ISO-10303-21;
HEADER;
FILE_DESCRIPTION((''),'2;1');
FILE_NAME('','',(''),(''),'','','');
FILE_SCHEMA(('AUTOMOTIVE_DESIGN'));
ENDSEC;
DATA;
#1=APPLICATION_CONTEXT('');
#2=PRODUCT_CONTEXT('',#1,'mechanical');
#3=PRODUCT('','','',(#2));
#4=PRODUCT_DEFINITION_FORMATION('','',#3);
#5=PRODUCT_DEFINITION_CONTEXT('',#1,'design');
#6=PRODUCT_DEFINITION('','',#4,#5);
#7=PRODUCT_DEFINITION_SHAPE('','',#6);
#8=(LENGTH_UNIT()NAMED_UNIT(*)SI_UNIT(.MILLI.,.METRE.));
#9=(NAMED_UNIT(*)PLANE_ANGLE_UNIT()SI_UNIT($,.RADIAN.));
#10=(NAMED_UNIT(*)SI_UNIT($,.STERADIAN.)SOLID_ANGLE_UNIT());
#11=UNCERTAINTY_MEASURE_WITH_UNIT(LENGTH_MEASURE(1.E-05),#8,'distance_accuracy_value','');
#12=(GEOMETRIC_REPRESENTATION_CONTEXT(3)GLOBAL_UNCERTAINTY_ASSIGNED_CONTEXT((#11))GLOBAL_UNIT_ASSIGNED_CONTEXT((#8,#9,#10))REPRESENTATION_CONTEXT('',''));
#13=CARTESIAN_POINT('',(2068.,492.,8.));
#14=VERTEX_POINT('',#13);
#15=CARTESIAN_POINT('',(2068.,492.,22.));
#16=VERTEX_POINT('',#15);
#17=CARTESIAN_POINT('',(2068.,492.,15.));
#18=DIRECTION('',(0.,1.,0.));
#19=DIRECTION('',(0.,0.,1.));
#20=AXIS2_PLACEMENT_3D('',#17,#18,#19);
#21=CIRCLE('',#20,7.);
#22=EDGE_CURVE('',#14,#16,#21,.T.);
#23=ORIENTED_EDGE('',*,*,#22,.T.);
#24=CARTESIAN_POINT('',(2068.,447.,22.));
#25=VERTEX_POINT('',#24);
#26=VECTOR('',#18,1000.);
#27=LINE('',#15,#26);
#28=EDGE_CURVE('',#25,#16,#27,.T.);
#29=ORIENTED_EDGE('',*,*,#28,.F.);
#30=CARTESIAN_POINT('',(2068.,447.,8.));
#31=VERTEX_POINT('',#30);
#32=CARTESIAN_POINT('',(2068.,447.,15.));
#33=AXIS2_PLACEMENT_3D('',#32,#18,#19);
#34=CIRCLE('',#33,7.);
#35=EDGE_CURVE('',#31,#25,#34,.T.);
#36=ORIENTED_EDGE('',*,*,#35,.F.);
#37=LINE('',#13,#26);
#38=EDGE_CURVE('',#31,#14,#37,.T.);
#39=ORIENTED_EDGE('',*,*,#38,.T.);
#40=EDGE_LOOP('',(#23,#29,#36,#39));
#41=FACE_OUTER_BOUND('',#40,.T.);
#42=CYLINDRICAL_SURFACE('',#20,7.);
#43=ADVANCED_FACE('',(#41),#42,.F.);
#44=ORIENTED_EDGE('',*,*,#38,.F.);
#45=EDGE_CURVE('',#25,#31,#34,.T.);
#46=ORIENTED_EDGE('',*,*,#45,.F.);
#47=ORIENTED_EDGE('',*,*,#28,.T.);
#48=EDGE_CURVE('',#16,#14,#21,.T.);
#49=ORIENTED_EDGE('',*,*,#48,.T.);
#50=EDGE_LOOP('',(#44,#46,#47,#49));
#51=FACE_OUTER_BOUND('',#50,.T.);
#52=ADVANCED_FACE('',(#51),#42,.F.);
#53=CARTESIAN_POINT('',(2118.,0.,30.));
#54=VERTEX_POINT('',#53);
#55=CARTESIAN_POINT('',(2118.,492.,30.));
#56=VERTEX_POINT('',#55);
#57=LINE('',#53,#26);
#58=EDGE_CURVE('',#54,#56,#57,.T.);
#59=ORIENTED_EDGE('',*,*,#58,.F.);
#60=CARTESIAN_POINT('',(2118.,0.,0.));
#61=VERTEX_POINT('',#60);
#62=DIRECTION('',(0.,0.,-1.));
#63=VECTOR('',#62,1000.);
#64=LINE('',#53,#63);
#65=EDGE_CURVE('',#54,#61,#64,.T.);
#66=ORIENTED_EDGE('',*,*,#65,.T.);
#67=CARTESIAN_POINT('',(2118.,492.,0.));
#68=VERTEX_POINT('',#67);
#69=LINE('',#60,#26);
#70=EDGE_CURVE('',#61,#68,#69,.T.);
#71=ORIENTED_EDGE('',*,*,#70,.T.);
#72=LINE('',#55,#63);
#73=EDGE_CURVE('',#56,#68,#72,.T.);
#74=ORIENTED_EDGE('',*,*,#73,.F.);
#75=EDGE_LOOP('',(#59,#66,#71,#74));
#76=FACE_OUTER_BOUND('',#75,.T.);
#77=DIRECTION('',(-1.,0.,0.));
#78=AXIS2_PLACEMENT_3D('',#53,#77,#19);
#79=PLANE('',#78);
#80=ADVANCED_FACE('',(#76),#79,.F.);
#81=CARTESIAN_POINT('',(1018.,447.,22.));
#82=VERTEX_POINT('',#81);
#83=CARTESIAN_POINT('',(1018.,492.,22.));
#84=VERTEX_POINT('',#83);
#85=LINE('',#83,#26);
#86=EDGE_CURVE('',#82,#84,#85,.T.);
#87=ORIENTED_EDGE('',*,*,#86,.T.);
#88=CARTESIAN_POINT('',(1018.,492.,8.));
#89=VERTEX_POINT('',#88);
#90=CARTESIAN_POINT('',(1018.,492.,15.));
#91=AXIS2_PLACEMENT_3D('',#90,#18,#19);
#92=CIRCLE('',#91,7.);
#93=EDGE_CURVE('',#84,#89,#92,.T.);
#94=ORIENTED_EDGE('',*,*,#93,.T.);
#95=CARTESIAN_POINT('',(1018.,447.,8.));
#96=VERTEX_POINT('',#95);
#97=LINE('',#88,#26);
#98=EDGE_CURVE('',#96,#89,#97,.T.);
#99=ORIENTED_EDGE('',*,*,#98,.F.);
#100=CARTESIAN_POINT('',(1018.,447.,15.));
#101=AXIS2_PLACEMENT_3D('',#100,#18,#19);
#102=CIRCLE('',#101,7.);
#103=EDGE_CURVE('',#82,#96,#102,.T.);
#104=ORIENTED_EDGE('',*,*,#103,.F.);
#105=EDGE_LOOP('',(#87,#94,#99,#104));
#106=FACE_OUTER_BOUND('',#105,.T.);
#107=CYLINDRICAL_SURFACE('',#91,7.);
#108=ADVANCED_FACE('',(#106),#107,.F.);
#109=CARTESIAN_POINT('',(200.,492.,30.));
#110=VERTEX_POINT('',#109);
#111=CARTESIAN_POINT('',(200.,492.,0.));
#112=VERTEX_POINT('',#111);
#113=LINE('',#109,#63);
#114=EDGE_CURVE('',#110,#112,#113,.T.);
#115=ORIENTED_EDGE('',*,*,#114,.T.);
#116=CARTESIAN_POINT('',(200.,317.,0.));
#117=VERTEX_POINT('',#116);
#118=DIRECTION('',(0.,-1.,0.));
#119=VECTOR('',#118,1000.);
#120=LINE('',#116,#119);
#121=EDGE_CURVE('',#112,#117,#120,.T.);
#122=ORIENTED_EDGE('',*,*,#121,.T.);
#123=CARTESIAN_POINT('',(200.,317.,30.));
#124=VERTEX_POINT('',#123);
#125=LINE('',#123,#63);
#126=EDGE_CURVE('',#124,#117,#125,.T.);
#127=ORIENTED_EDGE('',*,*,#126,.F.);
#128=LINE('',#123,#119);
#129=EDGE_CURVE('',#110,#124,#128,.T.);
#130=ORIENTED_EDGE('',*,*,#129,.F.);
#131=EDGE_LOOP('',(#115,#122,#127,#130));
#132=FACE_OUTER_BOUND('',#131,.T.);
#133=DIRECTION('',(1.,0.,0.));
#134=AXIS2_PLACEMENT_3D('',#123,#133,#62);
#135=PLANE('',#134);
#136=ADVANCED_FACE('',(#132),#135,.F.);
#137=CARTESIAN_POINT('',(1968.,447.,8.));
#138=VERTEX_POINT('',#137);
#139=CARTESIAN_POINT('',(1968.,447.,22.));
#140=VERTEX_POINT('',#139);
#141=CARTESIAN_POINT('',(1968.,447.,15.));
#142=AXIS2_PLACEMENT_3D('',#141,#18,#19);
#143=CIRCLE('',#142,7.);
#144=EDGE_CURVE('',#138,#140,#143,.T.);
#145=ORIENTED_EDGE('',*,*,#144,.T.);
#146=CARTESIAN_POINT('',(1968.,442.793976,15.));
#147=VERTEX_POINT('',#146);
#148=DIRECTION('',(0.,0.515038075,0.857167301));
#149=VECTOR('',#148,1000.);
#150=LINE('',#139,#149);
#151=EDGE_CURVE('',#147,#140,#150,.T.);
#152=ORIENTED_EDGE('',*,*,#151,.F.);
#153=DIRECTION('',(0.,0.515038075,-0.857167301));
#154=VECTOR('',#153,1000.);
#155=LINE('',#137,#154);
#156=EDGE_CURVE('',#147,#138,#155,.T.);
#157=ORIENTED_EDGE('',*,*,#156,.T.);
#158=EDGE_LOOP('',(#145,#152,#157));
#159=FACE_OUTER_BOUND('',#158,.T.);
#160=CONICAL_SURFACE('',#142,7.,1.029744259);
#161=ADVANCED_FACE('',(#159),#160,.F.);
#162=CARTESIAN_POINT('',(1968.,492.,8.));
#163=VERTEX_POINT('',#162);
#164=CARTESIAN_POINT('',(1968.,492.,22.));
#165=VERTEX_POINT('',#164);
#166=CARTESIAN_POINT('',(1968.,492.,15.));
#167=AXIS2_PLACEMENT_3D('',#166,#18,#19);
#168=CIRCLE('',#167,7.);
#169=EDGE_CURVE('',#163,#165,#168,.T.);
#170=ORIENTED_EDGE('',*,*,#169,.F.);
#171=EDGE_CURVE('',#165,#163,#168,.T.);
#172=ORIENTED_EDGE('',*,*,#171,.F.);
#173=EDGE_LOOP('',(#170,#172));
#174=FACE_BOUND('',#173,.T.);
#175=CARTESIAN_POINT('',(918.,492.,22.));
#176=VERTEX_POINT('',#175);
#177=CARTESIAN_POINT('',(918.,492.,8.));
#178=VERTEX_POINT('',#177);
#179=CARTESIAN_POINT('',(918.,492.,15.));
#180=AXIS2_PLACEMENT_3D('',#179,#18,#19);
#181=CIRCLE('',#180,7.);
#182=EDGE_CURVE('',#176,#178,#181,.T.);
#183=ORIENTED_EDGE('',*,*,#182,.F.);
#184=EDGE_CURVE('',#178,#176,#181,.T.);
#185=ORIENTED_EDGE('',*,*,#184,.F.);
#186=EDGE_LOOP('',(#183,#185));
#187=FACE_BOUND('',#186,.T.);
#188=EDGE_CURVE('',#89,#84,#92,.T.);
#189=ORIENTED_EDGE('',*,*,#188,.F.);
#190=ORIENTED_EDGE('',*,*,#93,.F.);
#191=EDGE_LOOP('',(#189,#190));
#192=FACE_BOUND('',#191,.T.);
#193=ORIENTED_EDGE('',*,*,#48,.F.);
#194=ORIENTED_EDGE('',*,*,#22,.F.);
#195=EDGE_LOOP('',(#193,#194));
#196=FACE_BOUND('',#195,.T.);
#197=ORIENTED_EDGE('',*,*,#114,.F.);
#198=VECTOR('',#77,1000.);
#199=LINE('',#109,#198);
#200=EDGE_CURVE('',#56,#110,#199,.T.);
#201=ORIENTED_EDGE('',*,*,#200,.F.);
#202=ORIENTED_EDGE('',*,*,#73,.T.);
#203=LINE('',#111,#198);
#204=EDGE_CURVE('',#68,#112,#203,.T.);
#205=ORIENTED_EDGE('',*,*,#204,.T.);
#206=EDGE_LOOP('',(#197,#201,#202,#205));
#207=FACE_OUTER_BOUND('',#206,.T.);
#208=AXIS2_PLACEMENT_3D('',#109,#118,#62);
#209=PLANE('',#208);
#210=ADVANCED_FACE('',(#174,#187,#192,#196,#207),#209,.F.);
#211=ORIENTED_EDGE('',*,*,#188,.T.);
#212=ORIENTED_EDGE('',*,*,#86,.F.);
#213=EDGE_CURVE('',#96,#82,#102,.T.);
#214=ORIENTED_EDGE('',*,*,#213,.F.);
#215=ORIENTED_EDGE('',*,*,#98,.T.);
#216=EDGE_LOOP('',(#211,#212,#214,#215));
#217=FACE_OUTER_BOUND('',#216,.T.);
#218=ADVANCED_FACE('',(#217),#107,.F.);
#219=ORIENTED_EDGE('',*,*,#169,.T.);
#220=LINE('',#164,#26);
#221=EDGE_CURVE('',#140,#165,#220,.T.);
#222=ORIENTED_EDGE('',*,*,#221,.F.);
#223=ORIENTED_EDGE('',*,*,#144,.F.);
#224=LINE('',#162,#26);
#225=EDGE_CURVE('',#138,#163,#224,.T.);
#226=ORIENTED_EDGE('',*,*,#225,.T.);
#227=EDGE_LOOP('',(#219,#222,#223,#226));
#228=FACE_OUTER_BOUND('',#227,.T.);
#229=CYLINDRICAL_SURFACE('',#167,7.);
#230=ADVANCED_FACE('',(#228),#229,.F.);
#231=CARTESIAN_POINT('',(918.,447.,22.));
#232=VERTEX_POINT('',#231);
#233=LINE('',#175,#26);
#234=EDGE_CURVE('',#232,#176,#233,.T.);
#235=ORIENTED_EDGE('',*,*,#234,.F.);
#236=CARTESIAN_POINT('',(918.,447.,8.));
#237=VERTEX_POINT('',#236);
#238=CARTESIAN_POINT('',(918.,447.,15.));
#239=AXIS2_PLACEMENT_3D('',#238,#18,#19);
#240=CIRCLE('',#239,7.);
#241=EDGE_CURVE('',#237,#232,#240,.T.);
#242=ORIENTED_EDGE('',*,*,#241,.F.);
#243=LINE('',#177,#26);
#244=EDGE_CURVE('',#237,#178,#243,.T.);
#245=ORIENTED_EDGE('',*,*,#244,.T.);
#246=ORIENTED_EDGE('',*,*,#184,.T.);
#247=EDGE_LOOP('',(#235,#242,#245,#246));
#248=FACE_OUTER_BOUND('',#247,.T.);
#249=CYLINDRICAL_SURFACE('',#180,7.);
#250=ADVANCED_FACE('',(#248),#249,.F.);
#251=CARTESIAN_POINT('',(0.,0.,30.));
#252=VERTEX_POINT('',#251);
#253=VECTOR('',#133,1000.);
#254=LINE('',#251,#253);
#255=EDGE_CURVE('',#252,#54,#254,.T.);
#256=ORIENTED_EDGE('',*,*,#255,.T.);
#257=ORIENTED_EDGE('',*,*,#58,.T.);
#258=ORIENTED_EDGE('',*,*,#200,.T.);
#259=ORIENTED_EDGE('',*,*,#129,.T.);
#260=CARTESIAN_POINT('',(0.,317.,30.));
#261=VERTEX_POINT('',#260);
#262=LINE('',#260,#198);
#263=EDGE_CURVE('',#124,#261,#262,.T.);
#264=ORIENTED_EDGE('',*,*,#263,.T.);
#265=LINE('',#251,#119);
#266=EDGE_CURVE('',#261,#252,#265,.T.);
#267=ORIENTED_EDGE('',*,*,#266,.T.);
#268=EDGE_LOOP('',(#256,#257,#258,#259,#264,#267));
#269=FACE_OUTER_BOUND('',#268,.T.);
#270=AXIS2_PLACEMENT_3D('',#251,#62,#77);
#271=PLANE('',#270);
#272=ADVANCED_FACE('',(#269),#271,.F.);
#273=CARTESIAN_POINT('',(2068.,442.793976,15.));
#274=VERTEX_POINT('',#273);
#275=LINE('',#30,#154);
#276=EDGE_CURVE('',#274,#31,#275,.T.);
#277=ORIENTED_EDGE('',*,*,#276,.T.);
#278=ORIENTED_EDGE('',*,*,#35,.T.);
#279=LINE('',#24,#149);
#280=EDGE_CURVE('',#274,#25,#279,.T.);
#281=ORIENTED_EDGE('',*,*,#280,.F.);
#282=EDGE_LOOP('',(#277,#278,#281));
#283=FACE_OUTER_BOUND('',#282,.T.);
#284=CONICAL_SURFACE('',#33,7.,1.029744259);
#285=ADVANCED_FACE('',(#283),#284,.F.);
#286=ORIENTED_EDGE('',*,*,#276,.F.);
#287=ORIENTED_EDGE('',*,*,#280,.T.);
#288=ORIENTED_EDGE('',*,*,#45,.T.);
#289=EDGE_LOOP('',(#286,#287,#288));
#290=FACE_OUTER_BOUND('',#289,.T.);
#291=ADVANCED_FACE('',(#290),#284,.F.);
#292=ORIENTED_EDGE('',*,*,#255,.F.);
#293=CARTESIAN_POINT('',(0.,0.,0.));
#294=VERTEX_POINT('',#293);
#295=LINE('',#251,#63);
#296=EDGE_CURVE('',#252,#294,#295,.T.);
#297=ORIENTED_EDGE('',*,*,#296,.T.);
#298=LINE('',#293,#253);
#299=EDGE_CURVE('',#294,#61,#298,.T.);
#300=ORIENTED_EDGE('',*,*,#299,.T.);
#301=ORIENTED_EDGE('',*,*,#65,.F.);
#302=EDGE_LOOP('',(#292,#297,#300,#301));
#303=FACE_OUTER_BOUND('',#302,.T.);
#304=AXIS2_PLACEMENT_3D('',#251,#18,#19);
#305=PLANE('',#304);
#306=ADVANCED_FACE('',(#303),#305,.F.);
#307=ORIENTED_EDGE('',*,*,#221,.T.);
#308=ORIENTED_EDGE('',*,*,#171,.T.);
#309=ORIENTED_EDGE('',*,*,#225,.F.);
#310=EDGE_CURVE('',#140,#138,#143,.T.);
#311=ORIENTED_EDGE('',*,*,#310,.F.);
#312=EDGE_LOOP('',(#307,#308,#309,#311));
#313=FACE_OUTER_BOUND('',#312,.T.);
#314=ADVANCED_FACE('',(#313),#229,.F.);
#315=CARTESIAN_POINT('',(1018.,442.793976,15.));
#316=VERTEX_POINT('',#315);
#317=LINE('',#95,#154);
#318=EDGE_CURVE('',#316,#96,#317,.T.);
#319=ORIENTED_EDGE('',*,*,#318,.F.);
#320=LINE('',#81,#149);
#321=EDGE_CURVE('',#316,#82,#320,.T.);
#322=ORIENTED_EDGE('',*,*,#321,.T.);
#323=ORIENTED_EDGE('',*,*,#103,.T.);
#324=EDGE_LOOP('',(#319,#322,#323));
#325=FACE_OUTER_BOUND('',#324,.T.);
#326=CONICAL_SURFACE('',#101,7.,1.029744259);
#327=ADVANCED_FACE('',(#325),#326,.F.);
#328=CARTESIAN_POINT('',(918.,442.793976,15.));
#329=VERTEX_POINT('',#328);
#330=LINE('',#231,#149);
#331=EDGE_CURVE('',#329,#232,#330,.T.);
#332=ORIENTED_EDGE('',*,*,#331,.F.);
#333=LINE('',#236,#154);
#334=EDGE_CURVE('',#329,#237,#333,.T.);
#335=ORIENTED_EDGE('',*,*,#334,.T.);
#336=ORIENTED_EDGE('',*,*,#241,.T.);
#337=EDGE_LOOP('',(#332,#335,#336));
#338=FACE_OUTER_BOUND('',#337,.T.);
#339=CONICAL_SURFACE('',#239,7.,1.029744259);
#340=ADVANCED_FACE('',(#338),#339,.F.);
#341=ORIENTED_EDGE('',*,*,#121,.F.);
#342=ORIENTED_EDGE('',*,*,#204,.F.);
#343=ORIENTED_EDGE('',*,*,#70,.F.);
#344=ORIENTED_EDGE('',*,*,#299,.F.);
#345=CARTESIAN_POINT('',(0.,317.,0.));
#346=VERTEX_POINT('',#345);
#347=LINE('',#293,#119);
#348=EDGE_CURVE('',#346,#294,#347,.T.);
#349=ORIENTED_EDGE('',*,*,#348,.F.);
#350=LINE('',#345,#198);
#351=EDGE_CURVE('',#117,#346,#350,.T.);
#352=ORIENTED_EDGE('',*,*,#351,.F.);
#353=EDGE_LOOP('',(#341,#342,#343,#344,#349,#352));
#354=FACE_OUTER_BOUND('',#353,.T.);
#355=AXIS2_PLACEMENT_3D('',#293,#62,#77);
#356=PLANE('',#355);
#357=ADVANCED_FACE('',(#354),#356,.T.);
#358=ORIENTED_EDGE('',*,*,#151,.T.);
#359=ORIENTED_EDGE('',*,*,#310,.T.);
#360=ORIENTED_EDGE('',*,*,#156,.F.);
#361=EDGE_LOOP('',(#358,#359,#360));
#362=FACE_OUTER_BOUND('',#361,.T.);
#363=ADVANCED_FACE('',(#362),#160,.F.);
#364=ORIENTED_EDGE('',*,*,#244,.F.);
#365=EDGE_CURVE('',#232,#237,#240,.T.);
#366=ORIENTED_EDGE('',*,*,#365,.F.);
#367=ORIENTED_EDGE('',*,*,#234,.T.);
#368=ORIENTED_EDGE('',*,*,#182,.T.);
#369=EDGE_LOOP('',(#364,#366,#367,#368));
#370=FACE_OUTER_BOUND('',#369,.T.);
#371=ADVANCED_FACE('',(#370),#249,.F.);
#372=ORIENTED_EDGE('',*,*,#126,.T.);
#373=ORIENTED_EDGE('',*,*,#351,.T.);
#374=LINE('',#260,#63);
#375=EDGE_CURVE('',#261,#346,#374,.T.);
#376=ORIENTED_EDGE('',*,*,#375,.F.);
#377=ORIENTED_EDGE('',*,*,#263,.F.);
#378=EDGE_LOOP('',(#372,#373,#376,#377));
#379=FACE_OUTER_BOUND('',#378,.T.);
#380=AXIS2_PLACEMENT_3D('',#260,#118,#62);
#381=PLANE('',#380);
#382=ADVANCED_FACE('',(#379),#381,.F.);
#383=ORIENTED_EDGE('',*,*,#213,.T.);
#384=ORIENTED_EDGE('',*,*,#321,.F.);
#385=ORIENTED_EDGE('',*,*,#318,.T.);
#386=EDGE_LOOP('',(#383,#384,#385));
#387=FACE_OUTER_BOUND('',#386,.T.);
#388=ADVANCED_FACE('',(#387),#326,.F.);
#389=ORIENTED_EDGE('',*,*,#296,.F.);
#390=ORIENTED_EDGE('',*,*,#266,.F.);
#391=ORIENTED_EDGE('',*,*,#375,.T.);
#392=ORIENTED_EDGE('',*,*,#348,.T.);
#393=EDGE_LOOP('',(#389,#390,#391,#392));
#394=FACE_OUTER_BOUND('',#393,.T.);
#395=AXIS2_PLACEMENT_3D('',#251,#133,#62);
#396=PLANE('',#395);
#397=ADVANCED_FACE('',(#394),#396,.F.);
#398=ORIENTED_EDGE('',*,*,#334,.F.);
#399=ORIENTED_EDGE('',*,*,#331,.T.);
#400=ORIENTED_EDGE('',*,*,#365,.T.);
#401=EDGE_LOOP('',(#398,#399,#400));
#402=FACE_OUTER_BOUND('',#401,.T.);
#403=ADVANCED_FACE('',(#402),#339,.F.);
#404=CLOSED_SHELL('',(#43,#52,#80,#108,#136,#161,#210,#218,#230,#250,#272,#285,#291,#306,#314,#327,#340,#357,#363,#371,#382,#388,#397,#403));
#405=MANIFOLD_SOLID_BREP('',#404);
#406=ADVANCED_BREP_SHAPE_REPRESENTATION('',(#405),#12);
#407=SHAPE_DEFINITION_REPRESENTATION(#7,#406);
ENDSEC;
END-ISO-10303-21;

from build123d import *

# Parameters (mm, degrees)
BOSS_EXTRUDE1_DEPTH    = 30
M16_TAPPED_HOLE1_D     = 14
M16_TAPPED_HOLE1_DEPTH = 45
M16_TAPPED_HOLE1_TIP   = 4.206024333


with BuildPart() as part:
    # Sketch1 → Boss-Extrude1 (new body)
    with BuildSketch(Plane.XY):
        Polygon((0, 317), (200, 317), (200, 492), (2118, 492), (2118, 0), (0, 0), align=None)
    extrude(amount=BOSS_EXTRUDE1_DEPTH)

    # M16 Tapped Hole1
    with Locations(Plane(origin=(918, 492, 15), x_dir=(0, 0, 1), z_dir=(0, 1, 0))):
        with Locations((0, 0), (0, 100), (0, 1150), (0, 1050)):
            Hole(M16_TAPPED_HOLE1_D / 2, depth=M16_TAPPED_HOLE1_DEPTH)
            with Locations((0, 0, -(M16_TAPPED_HOLE1_DEPTH + M16_TAPPED_HOLE1_TIP / 2))):  # 118° drill point
                Cone(0, M16_TAPPED_HOLE1_D / 2, M16_TAPPED_HOLE1_TIP, mode=Mode.SUBTRACT)


solid = part.part
